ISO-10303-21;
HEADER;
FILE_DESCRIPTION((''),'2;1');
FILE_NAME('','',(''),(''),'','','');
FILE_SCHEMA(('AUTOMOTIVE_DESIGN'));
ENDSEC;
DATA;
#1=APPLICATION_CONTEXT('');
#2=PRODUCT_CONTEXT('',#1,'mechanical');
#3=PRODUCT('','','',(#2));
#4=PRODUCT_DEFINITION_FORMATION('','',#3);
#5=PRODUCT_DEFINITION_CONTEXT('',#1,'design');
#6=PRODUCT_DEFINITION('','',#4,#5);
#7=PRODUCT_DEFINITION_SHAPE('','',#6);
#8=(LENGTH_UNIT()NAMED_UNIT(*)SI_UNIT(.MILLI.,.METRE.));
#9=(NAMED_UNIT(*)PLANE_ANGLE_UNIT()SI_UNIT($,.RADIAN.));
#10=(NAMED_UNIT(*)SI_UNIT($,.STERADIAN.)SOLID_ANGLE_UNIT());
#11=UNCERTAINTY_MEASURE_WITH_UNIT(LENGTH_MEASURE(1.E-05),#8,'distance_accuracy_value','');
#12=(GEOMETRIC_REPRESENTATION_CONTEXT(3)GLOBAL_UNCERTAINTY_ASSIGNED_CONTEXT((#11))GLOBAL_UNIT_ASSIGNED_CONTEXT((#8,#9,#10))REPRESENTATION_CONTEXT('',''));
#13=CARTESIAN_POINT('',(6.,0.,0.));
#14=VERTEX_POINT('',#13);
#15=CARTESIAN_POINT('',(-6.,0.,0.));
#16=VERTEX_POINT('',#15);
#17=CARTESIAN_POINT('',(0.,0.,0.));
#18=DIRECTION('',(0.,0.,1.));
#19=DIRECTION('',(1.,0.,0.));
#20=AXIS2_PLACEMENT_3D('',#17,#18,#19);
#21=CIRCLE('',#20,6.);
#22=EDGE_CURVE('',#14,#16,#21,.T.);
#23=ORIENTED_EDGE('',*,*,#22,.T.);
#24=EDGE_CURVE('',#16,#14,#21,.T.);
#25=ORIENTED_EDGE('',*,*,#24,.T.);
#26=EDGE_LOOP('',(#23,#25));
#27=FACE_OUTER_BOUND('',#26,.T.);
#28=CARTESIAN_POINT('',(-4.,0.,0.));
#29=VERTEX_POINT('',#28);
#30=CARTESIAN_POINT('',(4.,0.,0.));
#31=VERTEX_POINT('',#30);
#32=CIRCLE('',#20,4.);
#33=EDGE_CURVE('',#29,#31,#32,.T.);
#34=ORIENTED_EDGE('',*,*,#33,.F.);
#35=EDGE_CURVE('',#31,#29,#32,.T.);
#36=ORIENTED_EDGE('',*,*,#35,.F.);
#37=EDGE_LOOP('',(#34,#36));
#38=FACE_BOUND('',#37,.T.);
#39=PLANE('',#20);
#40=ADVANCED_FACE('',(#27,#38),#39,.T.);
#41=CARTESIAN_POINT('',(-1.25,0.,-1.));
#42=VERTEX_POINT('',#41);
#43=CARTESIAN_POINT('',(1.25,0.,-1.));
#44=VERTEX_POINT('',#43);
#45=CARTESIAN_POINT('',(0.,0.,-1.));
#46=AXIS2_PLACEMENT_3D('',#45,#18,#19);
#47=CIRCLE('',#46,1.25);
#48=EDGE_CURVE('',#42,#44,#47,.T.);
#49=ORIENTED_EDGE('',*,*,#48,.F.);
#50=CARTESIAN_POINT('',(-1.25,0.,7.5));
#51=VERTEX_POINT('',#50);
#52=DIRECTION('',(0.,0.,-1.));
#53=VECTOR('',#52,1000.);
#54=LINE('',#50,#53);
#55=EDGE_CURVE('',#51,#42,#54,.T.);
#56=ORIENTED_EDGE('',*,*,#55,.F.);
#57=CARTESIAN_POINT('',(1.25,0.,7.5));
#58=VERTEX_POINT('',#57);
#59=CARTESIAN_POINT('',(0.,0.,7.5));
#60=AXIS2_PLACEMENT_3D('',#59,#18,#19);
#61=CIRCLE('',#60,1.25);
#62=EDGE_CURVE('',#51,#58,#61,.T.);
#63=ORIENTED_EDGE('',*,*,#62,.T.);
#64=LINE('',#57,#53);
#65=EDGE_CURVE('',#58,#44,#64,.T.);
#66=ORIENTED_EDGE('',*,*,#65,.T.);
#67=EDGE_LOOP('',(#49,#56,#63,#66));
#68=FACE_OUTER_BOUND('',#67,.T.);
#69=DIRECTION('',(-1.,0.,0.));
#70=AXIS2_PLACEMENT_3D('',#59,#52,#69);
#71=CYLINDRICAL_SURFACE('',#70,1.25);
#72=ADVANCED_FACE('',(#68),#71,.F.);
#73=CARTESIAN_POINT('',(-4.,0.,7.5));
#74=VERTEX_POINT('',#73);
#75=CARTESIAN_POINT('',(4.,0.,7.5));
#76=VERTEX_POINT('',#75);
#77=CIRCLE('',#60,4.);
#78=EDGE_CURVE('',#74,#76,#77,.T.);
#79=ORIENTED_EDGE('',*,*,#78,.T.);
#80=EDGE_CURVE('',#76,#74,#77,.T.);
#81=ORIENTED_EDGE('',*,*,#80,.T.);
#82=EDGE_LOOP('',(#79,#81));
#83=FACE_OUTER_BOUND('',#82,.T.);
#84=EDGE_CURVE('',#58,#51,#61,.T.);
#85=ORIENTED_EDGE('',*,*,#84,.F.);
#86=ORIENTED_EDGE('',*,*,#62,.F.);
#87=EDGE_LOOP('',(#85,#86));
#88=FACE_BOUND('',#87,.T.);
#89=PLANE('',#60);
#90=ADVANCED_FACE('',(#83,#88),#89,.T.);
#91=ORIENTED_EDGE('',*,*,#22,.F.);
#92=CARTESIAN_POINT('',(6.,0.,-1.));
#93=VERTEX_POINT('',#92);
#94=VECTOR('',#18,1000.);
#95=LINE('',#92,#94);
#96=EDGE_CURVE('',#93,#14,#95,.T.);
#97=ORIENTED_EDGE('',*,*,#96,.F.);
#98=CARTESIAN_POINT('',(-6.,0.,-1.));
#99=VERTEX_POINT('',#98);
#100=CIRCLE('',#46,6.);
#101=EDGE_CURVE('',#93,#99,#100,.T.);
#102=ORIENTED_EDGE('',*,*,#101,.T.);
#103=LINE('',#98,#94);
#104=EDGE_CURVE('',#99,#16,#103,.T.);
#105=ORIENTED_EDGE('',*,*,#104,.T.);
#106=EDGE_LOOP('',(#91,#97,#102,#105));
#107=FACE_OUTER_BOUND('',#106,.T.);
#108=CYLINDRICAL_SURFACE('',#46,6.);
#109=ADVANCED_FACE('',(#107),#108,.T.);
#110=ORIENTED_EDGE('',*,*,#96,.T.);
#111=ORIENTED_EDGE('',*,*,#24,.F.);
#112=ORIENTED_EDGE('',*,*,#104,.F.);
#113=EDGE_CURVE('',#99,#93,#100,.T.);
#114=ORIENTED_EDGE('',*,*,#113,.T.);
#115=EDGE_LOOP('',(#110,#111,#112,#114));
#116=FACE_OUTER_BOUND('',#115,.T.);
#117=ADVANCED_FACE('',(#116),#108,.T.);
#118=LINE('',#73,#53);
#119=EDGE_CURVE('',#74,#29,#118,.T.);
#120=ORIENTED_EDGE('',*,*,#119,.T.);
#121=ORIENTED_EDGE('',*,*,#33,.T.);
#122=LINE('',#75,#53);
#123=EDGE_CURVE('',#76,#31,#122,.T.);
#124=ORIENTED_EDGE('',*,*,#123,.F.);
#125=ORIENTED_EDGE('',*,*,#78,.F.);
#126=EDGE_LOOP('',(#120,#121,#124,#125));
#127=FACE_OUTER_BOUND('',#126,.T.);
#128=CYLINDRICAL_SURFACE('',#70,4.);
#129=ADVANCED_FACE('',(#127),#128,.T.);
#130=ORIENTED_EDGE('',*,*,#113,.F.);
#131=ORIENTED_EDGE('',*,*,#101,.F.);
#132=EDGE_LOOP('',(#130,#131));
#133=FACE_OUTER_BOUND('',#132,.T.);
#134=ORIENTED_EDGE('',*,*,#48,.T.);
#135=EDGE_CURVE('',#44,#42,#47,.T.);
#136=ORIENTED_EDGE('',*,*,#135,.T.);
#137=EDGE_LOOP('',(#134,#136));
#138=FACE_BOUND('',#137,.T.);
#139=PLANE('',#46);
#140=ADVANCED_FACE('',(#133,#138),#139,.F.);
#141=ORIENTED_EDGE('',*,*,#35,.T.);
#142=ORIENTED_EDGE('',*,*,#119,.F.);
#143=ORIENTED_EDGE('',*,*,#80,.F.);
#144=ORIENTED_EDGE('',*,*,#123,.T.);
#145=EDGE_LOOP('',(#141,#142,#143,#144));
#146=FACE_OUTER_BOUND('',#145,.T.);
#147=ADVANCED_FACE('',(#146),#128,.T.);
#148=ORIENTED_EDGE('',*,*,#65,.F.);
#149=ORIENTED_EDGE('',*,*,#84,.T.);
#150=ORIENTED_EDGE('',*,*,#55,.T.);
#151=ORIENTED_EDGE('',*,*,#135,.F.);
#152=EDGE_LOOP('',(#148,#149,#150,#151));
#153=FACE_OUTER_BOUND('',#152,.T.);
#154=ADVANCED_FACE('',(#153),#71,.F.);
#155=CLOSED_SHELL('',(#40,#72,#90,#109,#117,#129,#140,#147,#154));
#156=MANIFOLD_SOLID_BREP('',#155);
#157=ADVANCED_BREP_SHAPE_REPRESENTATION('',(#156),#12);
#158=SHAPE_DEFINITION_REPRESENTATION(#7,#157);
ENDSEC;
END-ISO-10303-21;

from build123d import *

# Parameters (mm, degrees)
SKETCH_1_R      = 4
SKETCH_1_R_2    = 1.25
EXTRUDE_1_DEPTH = 7.5
EXTRUDE_START   = -1
SKETCH_2_R      = 6
SKETCH_2_R_2    = 1.25
EXTRUDE_2_DEPTH = 1


with BuildPart() as part:
    # 草图1 → 凸台-拉伸1 (new body)
    with BuildSketch(Plane.XY):
        Circle(SKETCH_1_R)
        Circle(SKETCH_1_R_2, mode=Mode.SUBTRACT)
    extrude(amount=EXTRUDE_1_DEPTH)

    # 草图2 → 凸台-拉伸2 (add)
    with BuildSketch(Plane.XY.offset(EXTRUDE_START)):
        Circle(SKETCH_2_R)
        Circle(SKETCH_2_R_2, mode=Mode.SUBTRACT)
    extrude(amount=EXTRUDE_2_DEPTH)


solid = part.part
